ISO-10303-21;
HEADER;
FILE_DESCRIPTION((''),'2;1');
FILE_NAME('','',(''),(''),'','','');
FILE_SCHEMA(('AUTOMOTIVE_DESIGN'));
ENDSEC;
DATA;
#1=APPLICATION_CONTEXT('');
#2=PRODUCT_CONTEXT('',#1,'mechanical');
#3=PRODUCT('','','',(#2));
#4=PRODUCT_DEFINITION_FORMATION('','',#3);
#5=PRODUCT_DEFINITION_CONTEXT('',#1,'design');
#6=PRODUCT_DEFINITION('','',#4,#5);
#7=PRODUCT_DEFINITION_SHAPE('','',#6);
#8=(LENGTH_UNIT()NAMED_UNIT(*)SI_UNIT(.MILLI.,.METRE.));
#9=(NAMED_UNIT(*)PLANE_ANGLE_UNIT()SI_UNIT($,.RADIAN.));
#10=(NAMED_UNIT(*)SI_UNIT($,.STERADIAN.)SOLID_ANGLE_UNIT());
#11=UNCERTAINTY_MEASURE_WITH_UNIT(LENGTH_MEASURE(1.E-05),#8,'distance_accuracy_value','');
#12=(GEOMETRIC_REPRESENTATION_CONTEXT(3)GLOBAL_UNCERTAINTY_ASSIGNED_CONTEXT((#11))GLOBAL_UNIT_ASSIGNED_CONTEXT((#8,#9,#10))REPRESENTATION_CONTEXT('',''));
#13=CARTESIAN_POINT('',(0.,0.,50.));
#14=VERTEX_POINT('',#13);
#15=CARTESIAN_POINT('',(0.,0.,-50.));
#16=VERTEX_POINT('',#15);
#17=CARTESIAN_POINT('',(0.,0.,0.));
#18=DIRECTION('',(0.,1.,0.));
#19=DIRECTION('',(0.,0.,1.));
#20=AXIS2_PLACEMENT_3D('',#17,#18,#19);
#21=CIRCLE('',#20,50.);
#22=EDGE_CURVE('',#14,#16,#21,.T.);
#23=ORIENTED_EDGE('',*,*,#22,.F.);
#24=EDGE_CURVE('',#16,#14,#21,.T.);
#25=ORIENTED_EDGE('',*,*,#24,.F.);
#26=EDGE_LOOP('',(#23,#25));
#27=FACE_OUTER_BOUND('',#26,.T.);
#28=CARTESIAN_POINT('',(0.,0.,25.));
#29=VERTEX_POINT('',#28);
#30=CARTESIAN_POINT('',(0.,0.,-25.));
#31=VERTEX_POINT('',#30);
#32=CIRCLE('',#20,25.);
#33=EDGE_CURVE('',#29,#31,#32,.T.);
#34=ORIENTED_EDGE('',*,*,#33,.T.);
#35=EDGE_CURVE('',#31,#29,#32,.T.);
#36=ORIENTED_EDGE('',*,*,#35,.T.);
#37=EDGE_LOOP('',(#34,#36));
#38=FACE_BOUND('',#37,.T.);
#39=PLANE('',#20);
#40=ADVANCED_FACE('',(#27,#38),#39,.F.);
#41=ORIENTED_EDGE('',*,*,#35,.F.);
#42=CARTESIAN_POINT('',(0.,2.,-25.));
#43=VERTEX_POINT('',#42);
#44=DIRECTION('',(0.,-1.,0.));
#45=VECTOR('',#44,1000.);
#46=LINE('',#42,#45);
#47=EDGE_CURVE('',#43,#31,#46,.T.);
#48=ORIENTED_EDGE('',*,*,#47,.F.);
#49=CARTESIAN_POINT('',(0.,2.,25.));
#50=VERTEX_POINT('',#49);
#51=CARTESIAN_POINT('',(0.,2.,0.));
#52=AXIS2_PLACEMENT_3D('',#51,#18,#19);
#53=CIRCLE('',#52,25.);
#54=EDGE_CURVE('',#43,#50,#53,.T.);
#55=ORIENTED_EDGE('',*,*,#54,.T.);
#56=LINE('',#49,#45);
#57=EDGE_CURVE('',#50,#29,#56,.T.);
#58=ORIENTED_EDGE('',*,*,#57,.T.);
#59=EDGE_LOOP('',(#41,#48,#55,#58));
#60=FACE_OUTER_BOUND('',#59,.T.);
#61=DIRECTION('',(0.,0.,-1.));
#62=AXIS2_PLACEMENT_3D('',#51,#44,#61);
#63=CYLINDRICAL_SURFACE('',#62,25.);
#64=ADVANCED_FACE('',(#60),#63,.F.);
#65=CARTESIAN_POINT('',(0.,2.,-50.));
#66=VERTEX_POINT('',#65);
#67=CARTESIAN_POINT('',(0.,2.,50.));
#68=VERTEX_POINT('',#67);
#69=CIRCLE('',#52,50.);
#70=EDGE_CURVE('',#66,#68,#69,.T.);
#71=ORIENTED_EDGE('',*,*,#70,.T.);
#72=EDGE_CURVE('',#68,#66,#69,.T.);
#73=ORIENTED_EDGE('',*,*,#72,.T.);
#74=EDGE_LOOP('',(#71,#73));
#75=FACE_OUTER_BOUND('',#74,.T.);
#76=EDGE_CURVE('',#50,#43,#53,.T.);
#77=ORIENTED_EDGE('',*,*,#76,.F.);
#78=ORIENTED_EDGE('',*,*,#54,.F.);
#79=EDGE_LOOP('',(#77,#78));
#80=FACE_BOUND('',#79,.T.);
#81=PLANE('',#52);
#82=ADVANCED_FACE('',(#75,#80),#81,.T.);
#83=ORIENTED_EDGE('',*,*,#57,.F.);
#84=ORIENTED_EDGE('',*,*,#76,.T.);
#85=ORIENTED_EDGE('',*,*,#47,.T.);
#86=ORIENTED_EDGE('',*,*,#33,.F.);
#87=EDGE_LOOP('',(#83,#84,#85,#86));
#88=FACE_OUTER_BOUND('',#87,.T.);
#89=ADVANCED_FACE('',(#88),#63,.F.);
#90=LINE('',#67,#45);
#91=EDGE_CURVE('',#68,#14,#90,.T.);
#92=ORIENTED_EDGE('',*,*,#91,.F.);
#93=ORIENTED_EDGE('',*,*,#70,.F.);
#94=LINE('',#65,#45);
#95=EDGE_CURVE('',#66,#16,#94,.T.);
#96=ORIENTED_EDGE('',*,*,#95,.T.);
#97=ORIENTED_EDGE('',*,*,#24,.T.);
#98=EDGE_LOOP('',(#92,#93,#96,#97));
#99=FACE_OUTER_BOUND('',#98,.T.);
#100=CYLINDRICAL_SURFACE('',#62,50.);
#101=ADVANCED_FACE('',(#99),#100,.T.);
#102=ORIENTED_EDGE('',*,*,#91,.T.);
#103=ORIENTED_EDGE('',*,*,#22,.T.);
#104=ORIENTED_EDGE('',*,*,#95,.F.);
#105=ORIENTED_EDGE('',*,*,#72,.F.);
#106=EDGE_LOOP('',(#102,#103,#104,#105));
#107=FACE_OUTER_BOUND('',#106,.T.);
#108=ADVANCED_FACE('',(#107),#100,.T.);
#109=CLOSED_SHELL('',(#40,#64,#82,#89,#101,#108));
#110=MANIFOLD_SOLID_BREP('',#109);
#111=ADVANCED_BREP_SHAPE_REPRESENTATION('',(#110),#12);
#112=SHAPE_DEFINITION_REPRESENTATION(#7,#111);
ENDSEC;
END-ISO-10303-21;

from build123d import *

# Parameters (mm, degrees)
SKETCH1_R           = 50
SKETCH1_R_2         = 25
BOSS_EXTRUDE1_DEPTH = 2


with BuildPart() as part:
    # Sketch1 → Boss-Extrude1 (new body)
    with BuildSketch(Plane(origin=(0, 0, 0), x_dir=(1, 0, 0), z_dir=(0, 1, 0))):
        with Locations(Location((0, 0, 0), (0, 0, 270))):
            Circle(SKETCH1_R)
        with Locations(Location((0, 0, 0), (0, 0, 270))):
            Circle(SKETCH1_R_2, mode=Mode.SUBTRACT)
    extrude(amount=BOSS_EXTRUDE1_DEPTH)


solid = part.part
